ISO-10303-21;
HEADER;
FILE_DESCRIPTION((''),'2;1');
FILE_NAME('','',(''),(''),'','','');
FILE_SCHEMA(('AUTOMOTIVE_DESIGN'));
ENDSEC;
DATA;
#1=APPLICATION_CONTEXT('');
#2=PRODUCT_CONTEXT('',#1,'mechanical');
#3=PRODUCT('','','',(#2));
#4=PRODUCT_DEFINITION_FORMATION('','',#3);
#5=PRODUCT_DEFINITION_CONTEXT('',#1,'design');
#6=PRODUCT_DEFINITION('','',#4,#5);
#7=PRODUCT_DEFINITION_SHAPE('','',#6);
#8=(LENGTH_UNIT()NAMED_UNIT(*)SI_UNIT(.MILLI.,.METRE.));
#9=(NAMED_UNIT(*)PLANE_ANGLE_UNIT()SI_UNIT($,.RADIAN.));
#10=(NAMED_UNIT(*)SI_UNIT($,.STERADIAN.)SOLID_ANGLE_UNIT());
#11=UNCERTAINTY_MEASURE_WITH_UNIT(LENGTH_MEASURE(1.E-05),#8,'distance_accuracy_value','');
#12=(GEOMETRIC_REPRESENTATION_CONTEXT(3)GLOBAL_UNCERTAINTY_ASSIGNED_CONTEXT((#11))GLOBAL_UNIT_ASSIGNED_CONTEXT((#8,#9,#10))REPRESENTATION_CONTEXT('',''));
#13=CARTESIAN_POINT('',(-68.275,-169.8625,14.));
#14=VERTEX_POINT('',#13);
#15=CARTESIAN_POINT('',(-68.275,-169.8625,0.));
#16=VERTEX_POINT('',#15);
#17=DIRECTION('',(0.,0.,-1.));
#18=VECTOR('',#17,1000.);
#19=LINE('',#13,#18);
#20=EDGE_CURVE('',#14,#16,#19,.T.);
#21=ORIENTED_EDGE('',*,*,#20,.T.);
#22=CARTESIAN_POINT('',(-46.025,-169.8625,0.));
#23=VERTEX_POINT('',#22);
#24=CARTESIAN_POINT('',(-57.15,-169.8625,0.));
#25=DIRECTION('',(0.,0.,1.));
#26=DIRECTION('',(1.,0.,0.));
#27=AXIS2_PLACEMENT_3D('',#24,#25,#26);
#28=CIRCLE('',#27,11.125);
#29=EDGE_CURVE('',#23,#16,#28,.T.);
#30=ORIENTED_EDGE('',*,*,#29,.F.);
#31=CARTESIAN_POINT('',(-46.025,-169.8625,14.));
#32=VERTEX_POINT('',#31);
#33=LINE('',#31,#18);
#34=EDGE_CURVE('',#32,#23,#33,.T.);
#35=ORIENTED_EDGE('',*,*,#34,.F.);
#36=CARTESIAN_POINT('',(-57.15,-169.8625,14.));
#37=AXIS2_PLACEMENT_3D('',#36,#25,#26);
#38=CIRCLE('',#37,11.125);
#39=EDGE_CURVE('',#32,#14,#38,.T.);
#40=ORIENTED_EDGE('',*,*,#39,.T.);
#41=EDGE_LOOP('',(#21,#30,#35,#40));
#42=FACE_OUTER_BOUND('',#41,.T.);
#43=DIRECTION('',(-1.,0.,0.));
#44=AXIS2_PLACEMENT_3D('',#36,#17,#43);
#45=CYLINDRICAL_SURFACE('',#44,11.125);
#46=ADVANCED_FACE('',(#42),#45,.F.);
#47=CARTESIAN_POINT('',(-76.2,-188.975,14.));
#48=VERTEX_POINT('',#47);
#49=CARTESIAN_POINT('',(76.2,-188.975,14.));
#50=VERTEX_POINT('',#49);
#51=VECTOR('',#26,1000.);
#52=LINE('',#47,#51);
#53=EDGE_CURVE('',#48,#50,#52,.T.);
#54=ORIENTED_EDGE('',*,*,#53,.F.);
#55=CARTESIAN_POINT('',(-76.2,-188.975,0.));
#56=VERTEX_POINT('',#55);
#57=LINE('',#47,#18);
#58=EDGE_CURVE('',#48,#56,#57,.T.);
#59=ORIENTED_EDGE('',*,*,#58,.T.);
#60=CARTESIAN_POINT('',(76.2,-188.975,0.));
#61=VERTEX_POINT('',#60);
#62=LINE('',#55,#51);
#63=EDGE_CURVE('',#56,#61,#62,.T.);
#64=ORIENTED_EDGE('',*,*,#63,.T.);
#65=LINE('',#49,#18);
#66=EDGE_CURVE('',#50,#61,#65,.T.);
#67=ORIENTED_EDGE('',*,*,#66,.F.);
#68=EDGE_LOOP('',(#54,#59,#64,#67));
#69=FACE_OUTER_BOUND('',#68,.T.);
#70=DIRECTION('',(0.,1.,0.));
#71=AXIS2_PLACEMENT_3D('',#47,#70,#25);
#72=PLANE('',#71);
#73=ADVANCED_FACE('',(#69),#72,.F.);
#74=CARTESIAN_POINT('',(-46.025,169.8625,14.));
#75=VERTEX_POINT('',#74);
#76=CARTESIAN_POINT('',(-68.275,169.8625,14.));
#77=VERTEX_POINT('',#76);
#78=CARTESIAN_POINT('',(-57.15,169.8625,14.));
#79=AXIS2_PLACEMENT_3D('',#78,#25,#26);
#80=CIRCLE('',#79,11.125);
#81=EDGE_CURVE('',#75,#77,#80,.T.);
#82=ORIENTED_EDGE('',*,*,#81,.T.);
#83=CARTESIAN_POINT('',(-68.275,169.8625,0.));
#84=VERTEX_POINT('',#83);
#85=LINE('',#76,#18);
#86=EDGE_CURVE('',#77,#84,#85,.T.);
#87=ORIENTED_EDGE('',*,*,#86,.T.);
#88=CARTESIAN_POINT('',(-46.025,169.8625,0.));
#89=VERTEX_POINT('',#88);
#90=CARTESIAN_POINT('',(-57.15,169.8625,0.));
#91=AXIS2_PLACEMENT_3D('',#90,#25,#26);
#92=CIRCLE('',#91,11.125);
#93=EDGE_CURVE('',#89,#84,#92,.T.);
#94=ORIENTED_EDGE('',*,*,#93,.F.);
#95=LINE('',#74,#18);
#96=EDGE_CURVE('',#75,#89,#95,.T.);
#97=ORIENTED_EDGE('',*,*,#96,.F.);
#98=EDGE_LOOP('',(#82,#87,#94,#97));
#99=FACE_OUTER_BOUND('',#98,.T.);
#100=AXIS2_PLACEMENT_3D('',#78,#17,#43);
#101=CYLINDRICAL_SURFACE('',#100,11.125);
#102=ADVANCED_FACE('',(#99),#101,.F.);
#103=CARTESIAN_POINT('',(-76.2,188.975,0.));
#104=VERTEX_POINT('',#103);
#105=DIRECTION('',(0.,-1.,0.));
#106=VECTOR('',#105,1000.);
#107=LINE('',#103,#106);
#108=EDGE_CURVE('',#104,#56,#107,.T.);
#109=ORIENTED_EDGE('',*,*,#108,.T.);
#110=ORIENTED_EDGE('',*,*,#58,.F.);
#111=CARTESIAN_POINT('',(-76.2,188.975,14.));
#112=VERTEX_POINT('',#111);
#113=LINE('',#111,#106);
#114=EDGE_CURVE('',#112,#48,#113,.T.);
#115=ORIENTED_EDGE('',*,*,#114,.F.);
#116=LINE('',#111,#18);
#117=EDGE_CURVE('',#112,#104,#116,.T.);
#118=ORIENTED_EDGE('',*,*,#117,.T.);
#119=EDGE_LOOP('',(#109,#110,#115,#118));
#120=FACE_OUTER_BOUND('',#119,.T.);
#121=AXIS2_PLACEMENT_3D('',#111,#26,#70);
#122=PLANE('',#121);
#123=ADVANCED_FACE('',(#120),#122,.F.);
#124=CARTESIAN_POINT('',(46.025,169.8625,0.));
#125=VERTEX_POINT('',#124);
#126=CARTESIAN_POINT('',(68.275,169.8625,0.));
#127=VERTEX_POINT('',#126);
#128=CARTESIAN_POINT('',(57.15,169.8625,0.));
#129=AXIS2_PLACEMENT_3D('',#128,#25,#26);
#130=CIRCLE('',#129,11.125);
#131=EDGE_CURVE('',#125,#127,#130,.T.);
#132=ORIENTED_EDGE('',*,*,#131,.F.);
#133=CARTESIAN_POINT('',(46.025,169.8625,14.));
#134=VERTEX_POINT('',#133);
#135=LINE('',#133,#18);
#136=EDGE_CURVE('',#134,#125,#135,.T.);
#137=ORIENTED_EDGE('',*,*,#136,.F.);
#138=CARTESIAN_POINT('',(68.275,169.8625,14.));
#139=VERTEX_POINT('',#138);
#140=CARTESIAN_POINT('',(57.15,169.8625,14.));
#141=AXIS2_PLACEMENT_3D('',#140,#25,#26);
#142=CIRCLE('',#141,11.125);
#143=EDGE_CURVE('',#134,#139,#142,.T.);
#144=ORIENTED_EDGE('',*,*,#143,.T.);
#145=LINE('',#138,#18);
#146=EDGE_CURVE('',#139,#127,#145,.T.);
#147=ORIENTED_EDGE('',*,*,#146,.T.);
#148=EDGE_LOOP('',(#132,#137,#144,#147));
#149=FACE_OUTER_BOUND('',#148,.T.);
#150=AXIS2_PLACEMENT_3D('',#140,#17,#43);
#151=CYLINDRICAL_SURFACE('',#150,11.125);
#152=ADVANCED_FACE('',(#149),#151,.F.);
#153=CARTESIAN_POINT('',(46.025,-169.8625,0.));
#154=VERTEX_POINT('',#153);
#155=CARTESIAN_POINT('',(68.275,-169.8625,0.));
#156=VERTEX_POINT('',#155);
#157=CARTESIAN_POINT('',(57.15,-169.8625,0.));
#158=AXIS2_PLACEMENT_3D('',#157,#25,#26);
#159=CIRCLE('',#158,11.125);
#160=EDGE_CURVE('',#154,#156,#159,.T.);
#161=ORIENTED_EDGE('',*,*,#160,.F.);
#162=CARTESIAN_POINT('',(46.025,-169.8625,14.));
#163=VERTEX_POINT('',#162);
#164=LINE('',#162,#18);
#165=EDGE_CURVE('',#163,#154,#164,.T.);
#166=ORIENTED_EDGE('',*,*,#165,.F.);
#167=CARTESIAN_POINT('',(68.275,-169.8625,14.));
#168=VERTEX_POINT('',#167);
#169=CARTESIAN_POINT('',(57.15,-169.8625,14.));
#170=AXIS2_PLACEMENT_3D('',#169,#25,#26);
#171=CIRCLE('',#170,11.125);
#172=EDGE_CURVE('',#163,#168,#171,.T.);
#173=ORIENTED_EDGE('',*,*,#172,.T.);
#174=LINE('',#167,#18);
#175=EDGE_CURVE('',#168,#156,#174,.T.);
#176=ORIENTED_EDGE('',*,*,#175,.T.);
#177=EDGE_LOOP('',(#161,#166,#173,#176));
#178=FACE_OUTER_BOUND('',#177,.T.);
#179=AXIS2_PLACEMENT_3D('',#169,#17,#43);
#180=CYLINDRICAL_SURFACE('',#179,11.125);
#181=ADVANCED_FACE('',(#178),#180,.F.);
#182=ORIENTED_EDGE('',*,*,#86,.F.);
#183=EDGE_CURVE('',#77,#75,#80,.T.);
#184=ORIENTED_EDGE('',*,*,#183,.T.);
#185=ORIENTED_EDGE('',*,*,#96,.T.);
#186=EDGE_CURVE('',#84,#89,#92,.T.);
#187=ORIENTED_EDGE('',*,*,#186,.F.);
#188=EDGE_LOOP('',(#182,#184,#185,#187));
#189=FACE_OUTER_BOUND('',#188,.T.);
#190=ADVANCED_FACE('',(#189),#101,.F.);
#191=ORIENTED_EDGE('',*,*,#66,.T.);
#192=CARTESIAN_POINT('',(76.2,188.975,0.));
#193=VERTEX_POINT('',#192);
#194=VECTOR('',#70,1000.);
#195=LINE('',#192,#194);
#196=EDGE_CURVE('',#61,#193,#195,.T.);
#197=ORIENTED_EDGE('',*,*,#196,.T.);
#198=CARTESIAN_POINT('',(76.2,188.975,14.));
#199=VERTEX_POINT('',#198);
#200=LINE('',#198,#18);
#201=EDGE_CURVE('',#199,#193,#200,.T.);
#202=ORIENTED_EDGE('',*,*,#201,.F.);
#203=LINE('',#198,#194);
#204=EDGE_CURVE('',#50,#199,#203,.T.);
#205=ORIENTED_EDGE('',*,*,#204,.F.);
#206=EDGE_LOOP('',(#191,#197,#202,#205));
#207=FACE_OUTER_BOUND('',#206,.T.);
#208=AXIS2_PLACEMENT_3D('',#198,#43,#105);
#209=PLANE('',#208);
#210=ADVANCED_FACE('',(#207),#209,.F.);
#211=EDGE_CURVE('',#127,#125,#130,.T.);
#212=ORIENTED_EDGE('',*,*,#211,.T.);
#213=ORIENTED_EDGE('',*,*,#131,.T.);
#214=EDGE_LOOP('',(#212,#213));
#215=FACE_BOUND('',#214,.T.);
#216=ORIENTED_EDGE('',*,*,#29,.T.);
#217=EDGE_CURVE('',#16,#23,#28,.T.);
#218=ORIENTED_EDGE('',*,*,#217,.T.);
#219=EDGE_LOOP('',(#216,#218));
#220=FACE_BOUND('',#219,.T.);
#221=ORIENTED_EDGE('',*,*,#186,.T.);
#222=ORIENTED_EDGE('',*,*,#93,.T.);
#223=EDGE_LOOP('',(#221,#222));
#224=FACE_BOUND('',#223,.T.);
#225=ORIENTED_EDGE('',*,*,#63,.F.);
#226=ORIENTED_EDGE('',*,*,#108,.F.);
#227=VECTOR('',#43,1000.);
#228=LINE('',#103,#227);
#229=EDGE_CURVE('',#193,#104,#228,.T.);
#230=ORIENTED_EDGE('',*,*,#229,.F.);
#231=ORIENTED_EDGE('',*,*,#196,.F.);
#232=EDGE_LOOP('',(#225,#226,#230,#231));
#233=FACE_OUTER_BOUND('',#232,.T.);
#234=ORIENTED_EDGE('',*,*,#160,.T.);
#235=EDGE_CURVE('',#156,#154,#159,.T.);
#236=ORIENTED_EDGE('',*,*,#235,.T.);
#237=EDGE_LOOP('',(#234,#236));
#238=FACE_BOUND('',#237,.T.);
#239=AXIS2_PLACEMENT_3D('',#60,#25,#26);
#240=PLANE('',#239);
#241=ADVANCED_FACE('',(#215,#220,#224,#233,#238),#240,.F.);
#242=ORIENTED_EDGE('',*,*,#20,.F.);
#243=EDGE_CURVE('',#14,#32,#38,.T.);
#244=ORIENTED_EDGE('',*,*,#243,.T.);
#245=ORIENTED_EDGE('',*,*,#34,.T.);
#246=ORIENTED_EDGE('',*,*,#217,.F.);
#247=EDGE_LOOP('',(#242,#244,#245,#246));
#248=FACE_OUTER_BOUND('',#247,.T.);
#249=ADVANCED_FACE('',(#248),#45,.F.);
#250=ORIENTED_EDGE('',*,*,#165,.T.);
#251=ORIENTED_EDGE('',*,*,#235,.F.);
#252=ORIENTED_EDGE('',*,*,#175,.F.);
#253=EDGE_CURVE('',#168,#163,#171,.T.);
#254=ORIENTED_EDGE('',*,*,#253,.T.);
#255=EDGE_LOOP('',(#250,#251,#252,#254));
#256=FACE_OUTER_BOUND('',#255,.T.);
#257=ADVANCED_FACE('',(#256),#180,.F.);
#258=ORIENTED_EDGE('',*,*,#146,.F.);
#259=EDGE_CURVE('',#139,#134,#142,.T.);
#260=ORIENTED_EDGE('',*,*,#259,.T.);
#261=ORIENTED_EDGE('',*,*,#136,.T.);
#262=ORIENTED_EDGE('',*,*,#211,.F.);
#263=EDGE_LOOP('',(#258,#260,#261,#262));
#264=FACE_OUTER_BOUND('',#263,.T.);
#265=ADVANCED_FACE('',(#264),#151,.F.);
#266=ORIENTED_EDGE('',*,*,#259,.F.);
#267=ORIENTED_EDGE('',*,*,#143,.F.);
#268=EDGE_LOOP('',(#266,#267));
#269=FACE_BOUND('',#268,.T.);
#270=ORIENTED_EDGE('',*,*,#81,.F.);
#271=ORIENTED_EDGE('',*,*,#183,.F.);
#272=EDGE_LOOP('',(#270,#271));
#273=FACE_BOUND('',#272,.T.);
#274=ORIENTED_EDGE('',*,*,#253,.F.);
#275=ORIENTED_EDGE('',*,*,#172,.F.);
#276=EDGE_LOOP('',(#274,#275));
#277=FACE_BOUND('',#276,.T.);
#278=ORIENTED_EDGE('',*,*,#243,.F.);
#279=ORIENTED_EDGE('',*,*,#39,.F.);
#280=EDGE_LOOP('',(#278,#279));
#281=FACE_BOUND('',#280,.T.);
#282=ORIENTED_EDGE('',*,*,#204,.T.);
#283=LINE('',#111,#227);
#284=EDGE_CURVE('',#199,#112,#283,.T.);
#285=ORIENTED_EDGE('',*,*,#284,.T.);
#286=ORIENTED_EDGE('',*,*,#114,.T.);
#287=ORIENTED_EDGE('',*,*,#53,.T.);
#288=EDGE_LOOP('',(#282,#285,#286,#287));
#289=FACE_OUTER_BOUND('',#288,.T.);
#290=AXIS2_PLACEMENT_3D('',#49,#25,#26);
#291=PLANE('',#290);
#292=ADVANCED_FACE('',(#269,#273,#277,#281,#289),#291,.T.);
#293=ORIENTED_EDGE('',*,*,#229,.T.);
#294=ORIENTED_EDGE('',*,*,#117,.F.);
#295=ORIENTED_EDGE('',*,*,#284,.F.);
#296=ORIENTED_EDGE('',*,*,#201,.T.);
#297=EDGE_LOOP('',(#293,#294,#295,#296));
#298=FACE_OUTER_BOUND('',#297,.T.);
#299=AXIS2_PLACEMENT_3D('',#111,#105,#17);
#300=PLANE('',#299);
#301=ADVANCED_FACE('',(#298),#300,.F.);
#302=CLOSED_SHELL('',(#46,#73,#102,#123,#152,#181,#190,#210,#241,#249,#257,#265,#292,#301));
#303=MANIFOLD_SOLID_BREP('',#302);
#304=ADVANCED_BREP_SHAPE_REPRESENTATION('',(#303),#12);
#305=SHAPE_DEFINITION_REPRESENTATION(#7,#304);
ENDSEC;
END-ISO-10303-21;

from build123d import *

# Parameters (mm, degrees)
SKETCH1_W           = 152.4
SKETCH1_H           = 377.95
SKETCH1_R           = 11.125
BOSS_EXTRUDE1_DEPTH = 14


with BuildPart() as part:
    # Sketch1 → Boss-Extrude1 (new body)
    with BuildSketch(Plane.XY):
        Rectangle(SKETCH1_W, SKETCH1_H)
        with Locations((-57.15, 169.8625)):
            Circle(SKETCH1_R, mode=Mode.SUBTRACT)
        with Locations((57.15, 169.8625)):
            Circle(SKETCH1_R, mode=Mode.SUBTRACT)
        with Locations((57.15, -169.8625)):
            Circle(SKETCH1_R, mode=Mode.SUBTRACT)
        with Locations((-57.15, -169.8625)):
            Circle(SKETCH1_R, mode=Mode.SUBTRACT)
    extrude(amount=BOSS_EXTRUDE1_DEPTH)


solid = part.part
